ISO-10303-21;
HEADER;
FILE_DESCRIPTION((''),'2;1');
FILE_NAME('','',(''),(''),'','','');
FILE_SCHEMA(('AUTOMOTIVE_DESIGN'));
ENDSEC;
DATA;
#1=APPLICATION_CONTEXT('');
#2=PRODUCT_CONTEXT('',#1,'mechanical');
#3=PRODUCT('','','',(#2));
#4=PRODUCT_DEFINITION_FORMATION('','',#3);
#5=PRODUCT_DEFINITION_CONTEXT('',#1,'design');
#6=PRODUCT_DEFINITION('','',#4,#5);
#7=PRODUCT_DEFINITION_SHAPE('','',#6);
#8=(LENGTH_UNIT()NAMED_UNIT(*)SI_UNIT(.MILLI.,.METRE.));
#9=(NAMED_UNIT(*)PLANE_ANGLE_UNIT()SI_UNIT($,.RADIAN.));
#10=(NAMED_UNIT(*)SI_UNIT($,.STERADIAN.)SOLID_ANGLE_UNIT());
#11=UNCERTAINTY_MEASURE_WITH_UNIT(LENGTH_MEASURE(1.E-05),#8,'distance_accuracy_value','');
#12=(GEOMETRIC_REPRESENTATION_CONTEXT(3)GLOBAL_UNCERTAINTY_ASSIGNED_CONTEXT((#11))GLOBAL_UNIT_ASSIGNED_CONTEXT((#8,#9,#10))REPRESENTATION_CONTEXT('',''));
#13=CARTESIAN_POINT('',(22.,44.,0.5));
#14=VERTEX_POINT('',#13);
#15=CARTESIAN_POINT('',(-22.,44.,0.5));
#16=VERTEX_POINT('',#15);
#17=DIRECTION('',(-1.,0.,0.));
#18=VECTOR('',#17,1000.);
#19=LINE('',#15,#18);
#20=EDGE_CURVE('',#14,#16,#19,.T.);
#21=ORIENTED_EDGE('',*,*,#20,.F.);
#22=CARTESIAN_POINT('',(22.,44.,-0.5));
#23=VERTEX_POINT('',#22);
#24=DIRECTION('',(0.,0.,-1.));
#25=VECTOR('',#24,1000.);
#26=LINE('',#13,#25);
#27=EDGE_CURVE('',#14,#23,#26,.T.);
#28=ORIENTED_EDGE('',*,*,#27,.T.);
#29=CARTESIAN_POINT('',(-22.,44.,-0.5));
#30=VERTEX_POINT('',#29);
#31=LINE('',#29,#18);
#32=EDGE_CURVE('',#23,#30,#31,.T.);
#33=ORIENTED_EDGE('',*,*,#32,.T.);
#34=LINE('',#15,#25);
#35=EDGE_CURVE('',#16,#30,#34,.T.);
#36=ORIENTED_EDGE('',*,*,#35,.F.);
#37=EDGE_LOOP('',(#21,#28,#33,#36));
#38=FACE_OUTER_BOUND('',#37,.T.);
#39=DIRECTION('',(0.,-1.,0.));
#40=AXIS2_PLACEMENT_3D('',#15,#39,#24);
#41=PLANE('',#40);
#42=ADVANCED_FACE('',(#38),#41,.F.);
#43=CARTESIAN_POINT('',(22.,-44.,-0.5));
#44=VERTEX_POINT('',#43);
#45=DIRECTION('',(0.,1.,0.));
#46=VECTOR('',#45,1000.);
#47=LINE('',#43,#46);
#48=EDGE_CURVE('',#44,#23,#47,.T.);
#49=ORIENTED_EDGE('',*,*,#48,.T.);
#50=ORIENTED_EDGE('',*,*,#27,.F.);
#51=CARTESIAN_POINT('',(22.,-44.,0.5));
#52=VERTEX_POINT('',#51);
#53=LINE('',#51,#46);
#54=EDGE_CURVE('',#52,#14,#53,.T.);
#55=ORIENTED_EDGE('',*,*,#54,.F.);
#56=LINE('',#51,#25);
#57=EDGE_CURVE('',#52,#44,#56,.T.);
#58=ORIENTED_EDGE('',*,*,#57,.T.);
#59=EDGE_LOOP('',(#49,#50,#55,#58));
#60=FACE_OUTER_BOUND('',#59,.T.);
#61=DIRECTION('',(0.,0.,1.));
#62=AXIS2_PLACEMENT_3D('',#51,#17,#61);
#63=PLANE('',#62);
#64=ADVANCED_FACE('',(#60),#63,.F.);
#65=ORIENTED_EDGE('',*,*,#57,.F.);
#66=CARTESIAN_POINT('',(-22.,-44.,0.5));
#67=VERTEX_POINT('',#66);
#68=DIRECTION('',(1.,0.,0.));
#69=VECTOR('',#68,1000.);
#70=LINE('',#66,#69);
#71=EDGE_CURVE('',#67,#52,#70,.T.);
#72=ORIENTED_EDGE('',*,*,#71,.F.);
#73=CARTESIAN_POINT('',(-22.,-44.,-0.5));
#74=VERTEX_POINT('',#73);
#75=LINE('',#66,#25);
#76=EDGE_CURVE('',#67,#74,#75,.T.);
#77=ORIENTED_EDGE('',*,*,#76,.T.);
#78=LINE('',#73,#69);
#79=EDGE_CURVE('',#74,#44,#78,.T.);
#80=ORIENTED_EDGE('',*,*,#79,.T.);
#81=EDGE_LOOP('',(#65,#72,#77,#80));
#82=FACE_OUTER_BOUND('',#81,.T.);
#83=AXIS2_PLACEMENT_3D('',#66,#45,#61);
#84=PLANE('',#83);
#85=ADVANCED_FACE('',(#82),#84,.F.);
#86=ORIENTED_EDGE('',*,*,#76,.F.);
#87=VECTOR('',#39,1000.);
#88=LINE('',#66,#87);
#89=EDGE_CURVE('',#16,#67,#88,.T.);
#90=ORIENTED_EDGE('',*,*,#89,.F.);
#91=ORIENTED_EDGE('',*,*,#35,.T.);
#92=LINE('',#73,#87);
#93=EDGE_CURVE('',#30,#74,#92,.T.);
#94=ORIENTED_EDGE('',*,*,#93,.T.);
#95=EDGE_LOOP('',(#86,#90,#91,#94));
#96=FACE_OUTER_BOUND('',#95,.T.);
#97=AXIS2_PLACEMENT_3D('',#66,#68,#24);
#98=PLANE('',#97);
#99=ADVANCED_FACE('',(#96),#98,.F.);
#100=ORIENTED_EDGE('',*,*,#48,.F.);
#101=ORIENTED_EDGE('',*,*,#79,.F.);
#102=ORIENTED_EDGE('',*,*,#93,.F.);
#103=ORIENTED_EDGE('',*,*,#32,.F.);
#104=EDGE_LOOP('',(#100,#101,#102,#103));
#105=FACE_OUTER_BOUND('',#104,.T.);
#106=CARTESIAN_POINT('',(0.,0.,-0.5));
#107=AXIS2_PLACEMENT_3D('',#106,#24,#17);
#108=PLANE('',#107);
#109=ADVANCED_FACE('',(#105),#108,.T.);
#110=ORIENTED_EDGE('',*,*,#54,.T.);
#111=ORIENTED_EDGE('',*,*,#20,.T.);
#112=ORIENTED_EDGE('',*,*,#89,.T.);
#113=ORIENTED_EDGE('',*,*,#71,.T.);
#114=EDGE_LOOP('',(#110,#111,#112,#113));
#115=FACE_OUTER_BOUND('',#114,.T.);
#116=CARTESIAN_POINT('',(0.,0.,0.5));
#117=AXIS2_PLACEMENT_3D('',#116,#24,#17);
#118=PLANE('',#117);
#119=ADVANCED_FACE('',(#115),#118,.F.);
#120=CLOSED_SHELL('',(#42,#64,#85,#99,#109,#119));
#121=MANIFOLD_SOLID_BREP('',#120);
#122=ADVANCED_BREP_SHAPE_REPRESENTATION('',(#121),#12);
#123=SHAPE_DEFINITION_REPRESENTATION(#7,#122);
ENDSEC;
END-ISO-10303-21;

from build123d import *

# Parameters (mm, degrees)
SKETCH_1_W      = 44
SKETCH_1_H      = 88
EXTRUDE_1_DEPTH = 0.5


with BuildPart() as part:
    # 草图1 → 凸台-拉伸1 (new, symmetric)
    with BuildSketch(Plane.XY):
        Rectangle(SKETCH_1_W, SKETCH_1_H)
    extrude(amount=EXTRUDE_1_DEPTH, both=True)


solid = part.part
